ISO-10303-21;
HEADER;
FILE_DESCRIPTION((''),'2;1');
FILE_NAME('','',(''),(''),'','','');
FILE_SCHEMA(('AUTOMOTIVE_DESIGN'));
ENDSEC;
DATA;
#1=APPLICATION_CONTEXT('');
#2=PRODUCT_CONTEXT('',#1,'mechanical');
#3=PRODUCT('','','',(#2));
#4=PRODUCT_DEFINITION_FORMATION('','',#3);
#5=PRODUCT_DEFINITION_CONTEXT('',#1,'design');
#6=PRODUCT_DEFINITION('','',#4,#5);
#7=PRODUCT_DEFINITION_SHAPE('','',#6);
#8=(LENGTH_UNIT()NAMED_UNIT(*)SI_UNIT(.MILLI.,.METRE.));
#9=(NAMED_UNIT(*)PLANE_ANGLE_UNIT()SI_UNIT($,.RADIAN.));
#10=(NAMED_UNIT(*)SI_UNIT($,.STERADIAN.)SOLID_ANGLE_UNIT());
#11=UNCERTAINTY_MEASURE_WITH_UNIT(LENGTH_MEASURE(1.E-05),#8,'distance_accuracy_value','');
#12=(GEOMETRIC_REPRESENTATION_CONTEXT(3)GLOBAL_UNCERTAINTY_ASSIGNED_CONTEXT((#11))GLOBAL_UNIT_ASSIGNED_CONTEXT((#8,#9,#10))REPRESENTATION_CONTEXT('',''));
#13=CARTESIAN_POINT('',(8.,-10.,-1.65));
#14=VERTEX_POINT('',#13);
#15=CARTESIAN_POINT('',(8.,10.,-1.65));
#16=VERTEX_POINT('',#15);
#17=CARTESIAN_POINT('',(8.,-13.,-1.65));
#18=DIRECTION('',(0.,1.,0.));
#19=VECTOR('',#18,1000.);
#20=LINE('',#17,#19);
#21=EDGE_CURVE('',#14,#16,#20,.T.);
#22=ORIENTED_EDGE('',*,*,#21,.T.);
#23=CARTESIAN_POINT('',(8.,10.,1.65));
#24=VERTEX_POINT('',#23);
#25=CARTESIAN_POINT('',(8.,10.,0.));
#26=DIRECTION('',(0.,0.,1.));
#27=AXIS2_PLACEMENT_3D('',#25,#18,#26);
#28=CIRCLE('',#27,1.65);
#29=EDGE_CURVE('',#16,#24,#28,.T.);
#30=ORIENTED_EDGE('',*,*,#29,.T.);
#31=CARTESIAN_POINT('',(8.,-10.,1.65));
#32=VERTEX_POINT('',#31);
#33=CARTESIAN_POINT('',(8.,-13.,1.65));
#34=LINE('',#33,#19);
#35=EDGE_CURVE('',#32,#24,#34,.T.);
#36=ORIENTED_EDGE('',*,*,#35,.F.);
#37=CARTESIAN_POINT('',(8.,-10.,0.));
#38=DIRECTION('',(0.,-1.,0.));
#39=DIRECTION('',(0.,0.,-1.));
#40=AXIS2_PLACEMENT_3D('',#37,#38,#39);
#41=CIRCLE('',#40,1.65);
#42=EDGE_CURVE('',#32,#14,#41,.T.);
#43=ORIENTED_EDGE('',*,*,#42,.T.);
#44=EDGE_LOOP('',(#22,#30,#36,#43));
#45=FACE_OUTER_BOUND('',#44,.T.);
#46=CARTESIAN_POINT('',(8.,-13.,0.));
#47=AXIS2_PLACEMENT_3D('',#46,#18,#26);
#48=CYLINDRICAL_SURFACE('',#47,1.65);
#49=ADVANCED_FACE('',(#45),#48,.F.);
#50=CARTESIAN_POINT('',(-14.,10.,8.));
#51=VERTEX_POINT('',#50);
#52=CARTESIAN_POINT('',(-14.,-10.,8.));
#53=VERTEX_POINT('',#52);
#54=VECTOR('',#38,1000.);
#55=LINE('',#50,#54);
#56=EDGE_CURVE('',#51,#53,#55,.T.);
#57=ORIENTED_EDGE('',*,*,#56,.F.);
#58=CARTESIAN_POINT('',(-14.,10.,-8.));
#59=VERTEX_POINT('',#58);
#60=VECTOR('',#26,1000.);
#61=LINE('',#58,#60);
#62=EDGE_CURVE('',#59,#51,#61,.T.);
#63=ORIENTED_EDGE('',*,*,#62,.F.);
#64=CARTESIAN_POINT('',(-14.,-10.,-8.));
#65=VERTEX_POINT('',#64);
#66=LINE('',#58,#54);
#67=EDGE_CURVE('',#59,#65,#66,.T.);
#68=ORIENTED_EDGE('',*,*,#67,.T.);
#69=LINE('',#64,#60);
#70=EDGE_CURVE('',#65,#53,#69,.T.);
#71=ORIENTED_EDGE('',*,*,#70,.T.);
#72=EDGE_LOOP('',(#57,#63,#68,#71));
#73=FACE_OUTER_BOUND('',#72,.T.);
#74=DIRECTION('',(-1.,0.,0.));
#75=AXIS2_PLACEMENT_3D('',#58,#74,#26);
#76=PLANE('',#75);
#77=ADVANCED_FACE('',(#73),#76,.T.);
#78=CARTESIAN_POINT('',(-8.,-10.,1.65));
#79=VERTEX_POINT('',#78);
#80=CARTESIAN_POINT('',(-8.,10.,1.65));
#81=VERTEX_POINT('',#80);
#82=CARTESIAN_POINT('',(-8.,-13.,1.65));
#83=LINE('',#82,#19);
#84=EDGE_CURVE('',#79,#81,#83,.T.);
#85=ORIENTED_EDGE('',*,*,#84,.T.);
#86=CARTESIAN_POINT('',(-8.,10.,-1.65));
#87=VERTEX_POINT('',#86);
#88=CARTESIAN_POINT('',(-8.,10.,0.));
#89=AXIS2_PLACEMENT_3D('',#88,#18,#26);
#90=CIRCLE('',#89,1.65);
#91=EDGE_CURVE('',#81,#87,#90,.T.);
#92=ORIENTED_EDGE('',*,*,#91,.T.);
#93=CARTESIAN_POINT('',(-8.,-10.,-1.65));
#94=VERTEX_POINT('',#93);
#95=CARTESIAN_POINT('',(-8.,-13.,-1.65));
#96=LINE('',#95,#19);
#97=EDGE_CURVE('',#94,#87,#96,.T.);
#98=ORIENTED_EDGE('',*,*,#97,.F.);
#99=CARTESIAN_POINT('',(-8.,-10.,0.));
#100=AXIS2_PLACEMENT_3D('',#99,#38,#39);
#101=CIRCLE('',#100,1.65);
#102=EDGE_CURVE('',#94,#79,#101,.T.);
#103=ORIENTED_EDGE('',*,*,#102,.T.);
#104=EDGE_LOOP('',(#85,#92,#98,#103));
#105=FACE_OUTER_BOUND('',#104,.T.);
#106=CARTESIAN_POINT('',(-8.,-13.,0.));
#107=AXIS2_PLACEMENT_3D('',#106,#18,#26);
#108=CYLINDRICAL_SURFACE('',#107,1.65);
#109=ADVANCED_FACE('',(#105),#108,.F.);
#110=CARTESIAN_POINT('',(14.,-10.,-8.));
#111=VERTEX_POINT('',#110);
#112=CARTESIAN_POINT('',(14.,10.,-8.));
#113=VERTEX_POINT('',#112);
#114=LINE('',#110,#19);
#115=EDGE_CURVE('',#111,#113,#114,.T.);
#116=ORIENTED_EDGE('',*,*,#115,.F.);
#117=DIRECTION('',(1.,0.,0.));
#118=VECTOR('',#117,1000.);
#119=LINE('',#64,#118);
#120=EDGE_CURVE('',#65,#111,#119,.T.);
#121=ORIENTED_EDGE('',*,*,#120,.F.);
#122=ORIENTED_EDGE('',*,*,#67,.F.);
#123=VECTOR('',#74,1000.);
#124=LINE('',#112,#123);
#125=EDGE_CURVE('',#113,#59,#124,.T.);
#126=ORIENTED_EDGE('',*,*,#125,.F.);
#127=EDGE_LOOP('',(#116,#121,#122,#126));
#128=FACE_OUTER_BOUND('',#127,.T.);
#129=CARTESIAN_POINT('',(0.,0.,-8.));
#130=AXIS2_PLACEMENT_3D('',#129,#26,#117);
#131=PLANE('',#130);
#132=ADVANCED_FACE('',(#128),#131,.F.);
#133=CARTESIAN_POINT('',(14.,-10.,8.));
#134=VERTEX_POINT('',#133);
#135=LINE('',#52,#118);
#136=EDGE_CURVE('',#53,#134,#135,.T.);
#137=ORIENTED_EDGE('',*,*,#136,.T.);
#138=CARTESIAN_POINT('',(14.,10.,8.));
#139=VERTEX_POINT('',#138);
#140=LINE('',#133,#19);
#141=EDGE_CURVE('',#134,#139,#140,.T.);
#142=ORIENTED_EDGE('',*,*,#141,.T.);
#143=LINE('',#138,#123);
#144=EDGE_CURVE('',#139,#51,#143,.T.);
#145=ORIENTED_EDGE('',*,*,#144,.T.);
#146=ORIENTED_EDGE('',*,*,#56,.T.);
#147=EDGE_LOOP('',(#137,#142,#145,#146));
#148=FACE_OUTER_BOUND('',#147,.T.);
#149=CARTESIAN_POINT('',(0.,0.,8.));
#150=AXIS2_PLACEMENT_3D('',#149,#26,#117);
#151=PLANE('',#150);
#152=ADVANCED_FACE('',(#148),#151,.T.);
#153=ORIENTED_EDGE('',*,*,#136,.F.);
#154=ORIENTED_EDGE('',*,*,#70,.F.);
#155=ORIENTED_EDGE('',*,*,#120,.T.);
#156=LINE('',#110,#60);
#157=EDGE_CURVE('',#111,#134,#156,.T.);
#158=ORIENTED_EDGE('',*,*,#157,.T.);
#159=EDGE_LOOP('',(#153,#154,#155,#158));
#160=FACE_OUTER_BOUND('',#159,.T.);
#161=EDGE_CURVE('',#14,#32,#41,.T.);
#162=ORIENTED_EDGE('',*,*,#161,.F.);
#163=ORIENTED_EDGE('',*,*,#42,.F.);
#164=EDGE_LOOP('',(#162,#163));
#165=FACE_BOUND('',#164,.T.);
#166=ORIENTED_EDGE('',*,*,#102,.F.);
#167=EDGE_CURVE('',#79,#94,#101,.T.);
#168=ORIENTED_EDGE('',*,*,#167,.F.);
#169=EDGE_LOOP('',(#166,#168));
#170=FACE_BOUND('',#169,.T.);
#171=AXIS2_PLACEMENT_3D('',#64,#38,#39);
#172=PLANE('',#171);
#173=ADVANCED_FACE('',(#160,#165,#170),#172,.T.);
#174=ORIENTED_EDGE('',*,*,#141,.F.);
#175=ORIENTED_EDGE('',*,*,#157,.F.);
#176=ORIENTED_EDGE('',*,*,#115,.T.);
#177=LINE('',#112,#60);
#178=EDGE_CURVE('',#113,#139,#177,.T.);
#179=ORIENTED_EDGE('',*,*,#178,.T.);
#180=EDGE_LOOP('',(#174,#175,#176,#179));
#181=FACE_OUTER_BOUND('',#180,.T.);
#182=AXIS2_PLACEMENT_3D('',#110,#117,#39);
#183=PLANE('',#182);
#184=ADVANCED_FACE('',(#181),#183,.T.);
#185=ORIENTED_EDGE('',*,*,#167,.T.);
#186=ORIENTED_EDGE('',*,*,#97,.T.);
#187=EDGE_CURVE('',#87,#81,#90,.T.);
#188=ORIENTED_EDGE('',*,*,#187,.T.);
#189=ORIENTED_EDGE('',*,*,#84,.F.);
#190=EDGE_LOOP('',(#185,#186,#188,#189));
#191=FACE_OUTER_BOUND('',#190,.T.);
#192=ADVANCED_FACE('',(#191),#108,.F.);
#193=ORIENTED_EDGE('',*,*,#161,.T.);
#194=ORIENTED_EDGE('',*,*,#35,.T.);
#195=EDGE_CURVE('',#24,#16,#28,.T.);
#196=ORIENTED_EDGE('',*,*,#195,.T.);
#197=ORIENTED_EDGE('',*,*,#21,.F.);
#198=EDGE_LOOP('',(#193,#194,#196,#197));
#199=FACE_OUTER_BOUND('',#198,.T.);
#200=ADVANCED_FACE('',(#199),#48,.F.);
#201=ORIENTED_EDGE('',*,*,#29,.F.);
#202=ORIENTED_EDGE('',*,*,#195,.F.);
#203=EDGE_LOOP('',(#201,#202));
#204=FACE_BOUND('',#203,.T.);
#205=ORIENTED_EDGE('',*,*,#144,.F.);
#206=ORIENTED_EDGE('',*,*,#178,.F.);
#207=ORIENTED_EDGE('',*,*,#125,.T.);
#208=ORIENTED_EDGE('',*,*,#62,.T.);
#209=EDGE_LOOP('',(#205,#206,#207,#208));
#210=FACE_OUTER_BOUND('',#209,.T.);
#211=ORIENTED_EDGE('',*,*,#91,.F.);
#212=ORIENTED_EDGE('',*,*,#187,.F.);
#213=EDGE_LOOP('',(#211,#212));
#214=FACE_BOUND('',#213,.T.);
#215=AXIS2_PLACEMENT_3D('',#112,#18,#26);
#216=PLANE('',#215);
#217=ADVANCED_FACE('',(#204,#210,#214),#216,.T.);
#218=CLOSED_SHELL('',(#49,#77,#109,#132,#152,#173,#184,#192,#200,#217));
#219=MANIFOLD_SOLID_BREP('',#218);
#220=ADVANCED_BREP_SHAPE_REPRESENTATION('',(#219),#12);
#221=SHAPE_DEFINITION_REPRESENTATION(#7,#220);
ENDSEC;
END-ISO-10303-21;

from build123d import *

# Parameters (mm, degrees)
SKETCH_1_W          = 28
SKETCH_1_H          = 20
EXTRUDE_1_DEPTH     = 8
SKETCH_2_R          = 1.65
CUT_EXTRUDE_1_DEPTH = 13


with BuildPart() as part:
    # 草图1 → 凸台-拉伸1 (new, symmetric)
    with BuildSketch(Plane.XY):
        Rectangle(SKETCH_1_W, SKETCH_1_H)
    extrude(amount=EXTRUDE_1_DEPTH, both=True)

    # 草图2 → 切除-拉伸1 (cut, symmetric)
    with BuildSketch(Plane(origin=(0, 0, 0), x_dir=(1, 0, 0), z_dir=(0, 1, 0))):
        with Locations(Location((-8, 0, 0), (0, 0, 270))):
            Circle(SKETCH_2_R)
        with Locations(Location((8, 0, 0), (0, 0, 270))):
            Circle(SKETCH_2_R)
    extrude(amount=CUT_EXTRUDE_1_DEPTH, both=True, mode=Mode.SUBTRACT)


solid = part.part
